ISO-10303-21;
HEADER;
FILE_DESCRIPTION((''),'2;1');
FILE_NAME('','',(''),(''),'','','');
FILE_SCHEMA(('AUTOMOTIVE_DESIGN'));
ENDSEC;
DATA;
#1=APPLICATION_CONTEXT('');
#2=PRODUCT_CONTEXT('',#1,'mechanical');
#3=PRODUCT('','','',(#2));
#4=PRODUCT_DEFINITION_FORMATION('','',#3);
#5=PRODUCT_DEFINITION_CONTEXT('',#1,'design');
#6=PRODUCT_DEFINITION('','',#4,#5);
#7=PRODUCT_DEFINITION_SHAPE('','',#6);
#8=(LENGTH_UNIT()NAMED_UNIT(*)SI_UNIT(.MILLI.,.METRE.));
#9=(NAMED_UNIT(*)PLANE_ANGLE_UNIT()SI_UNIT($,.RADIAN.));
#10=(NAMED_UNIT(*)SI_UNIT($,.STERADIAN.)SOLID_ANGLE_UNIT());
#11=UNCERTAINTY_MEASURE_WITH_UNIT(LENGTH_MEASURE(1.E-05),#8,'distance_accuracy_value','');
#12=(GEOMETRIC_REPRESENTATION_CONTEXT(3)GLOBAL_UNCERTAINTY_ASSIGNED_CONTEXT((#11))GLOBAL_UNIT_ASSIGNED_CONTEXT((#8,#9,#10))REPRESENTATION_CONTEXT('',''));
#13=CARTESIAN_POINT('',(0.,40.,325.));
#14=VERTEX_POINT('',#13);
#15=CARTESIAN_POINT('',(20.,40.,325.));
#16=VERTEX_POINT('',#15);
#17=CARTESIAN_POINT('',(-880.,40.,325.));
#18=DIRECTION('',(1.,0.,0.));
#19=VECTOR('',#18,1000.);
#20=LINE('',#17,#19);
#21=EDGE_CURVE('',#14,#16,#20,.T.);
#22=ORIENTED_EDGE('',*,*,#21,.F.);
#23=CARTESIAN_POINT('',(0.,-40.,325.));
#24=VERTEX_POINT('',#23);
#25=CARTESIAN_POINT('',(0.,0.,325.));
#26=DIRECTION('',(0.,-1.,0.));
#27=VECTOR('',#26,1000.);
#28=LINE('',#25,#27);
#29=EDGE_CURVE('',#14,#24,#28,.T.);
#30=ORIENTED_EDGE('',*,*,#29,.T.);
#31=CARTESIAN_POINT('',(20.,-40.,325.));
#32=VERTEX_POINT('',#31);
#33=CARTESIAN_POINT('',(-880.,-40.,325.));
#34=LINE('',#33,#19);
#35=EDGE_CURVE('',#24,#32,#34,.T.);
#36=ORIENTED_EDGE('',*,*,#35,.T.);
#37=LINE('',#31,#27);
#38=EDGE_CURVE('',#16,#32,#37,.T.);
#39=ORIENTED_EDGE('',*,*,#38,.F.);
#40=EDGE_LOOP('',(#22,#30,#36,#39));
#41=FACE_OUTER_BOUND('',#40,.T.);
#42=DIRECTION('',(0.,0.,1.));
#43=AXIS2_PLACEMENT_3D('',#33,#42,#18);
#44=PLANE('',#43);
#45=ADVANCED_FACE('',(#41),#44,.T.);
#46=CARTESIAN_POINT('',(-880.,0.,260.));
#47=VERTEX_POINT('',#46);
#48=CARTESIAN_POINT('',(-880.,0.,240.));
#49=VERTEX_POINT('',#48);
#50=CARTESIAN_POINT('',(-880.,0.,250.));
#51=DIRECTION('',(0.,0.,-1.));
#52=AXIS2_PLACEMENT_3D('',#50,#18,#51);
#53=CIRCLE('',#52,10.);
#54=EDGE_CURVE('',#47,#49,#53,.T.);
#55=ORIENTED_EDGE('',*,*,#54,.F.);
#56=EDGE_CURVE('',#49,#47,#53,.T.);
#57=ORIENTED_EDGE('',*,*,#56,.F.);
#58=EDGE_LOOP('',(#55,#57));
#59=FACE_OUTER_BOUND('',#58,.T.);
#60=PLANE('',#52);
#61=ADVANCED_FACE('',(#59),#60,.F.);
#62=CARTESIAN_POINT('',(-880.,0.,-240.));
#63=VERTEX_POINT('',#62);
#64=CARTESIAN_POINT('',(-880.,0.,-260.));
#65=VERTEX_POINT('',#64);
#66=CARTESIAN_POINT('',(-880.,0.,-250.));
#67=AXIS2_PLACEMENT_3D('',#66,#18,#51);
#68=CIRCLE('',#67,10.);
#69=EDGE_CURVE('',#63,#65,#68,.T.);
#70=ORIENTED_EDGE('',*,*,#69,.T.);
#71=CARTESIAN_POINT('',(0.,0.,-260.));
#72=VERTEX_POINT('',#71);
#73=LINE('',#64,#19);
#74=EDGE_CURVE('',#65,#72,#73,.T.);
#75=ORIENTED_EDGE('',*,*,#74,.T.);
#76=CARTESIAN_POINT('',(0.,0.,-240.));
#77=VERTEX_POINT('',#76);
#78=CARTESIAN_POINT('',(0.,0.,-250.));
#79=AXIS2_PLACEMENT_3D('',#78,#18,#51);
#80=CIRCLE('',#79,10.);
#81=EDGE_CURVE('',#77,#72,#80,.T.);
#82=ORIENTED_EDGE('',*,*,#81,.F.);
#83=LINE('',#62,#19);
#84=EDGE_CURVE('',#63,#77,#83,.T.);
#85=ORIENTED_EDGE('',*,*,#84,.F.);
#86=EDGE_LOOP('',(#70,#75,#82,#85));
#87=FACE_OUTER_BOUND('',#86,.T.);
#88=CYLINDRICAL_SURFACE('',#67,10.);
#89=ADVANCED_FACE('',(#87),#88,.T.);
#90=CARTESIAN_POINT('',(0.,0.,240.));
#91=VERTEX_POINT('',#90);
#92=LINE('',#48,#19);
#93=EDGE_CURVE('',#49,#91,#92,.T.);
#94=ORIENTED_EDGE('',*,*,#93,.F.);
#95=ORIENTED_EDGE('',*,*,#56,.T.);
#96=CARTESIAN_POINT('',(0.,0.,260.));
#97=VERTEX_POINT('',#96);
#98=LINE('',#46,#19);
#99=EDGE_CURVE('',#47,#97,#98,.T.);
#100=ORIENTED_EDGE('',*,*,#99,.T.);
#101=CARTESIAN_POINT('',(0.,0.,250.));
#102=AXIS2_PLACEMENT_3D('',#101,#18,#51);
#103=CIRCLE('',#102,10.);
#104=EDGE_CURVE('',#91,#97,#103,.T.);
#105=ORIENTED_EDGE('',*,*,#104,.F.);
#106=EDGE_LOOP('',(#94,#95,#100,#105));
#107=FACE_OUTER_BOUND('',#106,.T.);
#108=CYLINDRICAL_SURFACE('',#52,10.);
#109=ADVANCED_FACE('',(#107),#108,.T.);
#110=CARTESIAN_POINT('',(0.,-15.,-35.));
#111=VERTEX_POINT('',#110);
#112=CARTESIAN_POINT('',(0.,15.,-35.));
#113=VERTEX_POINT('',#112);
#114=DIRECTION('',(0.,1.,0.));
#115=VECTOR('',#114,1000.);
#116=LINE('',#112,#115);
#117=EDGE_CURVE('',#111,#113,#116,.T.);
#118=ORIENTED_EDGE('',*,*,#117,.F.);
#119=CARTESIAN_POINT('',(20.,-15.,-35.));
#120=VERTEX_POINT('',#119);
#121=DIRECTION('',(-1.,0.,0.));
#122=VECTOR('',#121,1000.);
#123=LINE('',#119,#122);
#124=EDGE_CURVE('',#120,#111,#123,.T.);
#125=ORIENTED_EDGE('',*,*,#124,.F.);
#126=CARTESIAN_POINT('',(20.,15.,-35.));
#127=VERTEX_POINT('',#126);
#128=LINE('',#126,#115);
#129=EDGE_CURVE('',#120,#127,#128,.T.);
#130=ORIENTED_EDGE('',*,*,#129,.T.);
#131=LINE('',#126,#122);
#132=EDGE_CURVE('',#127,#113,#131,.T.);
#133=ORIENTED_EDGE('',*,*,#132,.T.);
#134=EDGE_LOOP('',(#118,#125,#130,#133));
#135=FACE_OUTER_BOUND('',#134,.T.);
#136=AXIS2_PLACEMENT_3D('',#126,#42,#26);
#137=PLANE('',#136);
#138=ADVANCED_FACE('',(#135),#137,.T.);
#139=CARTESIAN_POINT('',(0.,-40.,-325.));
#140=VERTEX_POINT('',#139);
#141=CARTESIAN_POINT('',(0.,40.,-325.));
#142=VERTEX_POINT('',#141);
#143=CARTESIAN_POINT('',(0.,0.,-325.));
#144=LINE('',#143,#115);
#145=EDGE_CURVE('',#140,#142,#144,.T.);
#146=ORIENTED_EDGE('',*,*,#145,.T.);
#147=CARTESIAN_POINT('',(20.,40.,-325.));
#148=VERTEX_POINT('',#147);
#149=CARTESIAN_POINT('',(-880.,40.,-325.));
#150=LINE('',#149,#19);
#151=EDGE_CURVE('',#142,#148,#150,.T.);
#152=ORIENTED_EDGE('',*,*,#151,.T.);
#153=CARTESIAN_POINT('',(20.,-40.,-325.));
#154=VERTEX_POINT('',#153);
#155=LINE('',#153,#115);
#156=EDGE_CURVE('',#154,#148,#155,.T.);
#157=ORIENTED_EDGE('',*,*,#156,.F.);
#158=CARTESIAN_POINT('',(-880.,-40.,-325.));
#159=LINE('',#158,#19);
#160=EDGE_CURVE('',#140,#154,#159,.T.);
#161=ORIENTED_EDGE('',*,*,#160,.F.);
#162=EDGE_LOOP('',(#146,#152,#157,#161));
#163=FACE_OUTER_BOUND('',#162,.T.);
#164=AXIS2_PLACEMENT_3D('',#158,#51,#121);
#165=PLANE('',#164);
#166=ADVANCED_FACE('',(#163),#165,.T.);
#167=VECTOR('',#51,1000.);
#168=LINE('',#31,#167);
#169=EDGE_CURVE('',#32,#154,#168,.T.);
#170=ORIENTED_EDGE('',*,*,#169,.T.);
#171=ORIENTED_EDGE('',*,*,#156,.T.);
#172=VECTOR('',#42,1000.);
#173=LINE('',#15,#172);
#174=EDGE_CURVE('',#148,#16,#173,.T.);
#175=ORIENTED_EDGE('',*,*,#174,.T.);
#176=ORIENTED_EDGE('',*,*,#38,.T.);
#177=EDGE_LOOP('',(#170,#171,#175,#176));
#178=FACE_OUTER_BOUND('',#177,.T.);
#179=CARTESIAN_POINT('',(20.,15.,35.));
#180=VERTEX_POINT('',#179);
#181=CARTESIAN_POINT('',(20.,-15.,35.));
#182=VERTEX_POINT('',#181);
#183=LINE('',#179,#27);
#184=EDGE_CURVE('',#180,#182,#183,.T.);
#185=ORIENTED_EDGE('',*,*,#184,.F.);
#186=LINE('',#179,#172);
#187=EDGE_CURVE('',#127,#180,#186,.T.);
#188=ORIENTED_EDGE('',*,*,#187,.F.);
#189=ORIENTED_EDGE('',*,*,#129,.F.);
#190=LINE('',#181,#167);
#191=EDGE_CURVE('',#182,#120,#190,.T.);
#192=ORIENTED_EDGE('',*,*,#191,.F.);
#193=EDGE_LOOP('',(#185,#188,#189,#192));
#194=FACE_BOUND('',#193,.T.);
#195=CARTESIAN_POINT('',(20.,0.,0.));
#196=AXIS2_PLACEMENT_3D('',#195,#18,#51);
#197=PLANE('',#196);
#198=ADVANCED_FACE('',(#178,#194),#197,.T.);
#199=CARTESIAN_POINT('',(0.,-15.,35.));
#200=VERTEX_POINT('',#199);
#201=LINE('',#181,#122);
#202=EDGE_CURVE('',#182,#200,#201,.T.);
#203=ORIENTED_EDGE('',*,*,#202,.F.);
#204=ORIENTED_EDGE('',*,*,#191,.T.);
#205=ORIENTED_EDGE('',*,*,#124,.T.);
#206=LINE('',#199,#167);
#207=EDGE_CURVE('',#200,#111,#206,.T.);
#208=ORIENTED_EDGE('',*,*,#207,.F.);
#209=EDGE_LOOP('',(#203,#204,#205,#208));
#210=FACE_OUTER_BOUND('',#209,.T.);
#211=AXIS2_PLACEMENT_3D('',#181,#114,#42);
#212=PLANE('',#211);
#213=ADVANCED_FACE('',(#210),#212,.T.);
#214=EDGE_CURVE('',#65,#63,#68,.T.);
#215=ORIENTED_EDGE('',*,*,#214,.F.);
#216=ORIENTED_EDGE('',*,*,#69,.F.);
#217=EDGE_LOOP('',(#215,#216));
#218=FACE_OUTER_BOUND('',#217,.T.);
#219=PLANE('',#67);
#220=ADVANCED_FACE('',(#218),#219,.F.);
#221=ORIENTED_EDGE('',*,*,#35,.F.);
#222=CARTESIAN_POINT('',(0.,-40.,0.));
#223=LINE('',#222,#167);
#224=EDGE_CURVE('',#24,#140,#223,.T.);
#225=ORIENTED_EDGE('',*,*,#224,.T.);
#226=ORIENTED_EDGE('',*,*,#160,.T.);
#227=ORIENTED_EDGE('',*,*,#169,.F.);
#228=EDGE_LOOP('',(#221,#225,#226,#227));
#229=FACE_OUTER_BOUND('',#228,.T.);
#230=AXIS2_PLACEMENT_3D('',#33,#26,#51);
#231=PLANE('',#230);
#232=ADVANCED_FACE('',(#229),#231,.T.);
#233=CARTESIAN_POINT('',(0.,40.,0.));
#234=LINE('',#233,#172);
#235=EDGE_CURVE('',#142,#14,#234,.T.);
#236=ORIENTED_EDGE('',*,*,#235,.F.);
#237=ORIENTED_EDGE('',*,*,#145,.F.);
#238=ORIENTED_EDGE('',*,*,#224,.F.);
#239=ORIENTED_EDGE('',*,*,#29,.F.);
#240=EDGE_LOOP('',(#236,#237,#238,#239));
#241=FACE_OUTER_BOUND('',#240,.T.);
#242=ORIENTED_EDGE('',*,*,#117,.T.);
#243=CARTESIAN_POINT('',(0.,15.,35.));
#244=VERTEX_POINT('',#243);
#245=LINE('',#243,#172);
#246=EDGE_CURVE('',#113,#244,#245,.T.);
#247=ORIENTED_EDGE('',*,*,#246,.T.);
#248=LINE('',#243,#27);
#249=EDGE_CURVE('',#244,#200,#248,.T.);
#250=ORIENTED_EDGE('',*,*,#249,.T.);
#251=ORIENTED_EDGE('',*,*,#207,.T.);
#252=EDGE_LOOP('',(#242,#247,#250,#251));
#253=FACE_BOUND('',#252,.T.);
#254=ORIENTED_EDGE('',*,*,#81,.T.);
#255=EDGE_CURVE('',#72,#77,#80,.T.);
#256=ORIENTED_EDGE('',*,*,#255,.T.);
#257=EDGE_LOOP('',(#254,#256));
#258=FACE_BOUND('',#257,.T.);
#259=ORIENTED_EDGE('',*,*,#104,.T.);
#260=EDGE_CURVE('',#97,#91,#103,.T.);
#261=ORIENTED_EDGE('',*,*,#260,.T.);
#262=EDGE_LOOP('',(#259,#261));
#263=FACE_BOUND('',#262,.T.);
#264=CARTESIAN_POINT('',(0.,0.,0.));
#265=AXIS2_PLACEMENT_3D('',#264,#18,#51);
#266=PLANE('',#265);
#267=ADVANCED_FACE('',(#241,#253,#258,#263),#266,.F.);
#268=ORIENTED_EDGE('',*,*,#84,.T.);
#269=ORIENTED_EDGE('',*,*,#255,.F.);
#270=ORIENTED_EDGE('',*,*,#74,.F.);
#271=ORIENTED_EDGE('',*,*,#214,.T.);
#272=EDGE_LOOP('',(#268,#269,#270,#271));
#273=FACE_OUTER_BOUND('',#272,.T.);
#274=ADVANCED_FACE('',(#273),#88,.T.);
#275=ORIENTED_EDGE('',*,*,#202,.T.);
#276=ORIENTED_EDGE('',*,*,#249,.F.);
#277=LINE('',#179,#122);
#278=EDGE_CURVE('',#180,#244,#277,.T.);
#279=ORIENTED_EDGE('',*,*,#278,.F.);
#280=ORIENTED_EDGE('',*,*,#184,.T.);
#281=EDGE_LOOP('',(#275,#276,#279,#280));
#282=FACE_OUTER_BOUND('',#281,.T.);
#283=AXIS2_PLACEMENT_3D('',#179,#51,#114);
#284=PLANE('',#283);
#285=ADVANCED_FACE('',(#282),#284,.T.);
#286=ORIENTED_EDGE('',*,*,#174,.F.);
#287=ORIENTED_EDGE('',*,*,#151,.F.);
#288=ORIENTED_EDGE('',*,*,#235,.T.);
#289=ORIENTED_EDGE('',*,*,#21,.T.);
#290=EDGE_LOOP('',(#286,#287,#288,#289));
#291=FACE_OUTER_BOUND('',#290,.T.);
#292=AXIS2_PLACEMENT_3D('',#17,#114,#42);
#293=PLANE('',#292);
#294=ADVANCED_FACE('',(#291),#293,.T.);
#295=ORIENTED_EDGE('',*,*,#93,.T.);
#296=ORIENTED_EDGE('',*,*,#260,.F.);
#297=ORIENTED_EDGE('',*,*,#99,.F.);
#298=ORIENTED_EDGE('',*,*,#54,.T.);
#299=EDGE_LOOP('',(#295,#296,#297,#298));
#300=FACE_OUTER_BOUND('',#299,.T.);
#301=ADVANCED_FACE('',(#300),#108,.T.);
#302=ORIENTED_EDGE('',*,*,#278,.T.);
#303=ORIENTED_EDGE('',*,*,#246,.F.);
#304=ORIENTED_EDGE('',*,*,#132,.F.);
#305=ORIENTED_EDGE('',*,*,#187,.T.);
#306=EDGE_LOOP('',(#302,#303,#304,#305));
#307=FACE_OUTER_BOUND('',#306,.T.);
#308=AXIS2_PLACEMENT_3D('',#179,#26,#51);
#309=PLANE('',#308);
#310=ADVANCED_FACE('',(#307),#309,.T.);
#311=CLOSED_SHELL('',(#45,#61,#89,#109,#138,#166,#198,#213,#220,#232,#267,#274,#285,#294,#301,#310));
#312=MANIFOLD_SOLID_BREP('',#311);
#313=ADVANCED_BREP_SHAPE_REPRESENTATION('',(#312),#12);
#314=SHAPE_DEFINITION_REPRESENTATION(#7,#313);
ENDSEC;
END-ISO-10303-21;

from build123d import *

# Parameters (mm, degrees)
SKETCH1_W           = 660
SKETCH1_H           = 90
SKETCH1_R           = 10
SKETCH1_W_2         = 70
SKETCH1_H_2         = 30
BOSS_EXTRUDE1_DEPTH = 20
BOSS_EXTRUDE2_START = -900
SKETCH2_R           = 10
BOSS_EXTRUDE2_DEPTH = 900
SKETCH3_W           = 903.641141734
SKETCH3_H           = 235.635140662
SKETCH3_W_2         = 650
SKETCH3_H_2         = 80
CUT_EXTRUDE1_DEPTH  = 960.648373103


with BuildPart() as part:
    # Sketch1 → Boss-Extrude1 (new body)
    with BuildSketch(Plane(origin=(0, 0, 0), x_dir=(0, 0, -1), z_dir=(1, 0, 0))):
        Rectangle(SKETCH1_W, SKETCH1_H)
        with Locations((-250, 0)):
            Circle(SKETCH1_R, mode=Mode.SUBTRACT)
        with Locations((250, 0)):
            Circle(SKETCH1_R, mode=Mode.SUBTRACT)
        Rectangle(SKETCH1_W_2, SKETCH1_H_2, mode=Mode.SUBTRACT)
    extrude(amount=BOSS_EXTRUDE1_DEPTH)

    # Sketch2 → Boss-Extrude2 (add)
    with BuildSketch(Plane(origin=(20, 0, 0), x_dir=(0, 0, -1), z_dir=(1, 0, 0)).offset(BOSS_EXTRUDE2_START)):
        with Locations((-250, 0)):
            Circle(SKETCH2_R)
        with Locations((250, 0)):
            Circle(SKETCH2_R)
    extrude(amount=BOSS_EXTRUDE2_DEPTH)

    # Sketch3 → Cut-Extrude1 (cut, through all)
    with BuildSketch(Plane(origin=(20, 0, 0), x_dir=(0, 0, -1), z_dir=(1, 0, 0))):
        Rectangle(SKETCH3_W, SKETCH3_H)
        Rectangle(SKETCH3_W_2, SKETCH3_H_2, mode=Mode.SUBTRACT)
    extrude(amount=-CUT_EXTRUDE1_DEPTH, mode=Mode.SUBTRACT)


solid = part.part
